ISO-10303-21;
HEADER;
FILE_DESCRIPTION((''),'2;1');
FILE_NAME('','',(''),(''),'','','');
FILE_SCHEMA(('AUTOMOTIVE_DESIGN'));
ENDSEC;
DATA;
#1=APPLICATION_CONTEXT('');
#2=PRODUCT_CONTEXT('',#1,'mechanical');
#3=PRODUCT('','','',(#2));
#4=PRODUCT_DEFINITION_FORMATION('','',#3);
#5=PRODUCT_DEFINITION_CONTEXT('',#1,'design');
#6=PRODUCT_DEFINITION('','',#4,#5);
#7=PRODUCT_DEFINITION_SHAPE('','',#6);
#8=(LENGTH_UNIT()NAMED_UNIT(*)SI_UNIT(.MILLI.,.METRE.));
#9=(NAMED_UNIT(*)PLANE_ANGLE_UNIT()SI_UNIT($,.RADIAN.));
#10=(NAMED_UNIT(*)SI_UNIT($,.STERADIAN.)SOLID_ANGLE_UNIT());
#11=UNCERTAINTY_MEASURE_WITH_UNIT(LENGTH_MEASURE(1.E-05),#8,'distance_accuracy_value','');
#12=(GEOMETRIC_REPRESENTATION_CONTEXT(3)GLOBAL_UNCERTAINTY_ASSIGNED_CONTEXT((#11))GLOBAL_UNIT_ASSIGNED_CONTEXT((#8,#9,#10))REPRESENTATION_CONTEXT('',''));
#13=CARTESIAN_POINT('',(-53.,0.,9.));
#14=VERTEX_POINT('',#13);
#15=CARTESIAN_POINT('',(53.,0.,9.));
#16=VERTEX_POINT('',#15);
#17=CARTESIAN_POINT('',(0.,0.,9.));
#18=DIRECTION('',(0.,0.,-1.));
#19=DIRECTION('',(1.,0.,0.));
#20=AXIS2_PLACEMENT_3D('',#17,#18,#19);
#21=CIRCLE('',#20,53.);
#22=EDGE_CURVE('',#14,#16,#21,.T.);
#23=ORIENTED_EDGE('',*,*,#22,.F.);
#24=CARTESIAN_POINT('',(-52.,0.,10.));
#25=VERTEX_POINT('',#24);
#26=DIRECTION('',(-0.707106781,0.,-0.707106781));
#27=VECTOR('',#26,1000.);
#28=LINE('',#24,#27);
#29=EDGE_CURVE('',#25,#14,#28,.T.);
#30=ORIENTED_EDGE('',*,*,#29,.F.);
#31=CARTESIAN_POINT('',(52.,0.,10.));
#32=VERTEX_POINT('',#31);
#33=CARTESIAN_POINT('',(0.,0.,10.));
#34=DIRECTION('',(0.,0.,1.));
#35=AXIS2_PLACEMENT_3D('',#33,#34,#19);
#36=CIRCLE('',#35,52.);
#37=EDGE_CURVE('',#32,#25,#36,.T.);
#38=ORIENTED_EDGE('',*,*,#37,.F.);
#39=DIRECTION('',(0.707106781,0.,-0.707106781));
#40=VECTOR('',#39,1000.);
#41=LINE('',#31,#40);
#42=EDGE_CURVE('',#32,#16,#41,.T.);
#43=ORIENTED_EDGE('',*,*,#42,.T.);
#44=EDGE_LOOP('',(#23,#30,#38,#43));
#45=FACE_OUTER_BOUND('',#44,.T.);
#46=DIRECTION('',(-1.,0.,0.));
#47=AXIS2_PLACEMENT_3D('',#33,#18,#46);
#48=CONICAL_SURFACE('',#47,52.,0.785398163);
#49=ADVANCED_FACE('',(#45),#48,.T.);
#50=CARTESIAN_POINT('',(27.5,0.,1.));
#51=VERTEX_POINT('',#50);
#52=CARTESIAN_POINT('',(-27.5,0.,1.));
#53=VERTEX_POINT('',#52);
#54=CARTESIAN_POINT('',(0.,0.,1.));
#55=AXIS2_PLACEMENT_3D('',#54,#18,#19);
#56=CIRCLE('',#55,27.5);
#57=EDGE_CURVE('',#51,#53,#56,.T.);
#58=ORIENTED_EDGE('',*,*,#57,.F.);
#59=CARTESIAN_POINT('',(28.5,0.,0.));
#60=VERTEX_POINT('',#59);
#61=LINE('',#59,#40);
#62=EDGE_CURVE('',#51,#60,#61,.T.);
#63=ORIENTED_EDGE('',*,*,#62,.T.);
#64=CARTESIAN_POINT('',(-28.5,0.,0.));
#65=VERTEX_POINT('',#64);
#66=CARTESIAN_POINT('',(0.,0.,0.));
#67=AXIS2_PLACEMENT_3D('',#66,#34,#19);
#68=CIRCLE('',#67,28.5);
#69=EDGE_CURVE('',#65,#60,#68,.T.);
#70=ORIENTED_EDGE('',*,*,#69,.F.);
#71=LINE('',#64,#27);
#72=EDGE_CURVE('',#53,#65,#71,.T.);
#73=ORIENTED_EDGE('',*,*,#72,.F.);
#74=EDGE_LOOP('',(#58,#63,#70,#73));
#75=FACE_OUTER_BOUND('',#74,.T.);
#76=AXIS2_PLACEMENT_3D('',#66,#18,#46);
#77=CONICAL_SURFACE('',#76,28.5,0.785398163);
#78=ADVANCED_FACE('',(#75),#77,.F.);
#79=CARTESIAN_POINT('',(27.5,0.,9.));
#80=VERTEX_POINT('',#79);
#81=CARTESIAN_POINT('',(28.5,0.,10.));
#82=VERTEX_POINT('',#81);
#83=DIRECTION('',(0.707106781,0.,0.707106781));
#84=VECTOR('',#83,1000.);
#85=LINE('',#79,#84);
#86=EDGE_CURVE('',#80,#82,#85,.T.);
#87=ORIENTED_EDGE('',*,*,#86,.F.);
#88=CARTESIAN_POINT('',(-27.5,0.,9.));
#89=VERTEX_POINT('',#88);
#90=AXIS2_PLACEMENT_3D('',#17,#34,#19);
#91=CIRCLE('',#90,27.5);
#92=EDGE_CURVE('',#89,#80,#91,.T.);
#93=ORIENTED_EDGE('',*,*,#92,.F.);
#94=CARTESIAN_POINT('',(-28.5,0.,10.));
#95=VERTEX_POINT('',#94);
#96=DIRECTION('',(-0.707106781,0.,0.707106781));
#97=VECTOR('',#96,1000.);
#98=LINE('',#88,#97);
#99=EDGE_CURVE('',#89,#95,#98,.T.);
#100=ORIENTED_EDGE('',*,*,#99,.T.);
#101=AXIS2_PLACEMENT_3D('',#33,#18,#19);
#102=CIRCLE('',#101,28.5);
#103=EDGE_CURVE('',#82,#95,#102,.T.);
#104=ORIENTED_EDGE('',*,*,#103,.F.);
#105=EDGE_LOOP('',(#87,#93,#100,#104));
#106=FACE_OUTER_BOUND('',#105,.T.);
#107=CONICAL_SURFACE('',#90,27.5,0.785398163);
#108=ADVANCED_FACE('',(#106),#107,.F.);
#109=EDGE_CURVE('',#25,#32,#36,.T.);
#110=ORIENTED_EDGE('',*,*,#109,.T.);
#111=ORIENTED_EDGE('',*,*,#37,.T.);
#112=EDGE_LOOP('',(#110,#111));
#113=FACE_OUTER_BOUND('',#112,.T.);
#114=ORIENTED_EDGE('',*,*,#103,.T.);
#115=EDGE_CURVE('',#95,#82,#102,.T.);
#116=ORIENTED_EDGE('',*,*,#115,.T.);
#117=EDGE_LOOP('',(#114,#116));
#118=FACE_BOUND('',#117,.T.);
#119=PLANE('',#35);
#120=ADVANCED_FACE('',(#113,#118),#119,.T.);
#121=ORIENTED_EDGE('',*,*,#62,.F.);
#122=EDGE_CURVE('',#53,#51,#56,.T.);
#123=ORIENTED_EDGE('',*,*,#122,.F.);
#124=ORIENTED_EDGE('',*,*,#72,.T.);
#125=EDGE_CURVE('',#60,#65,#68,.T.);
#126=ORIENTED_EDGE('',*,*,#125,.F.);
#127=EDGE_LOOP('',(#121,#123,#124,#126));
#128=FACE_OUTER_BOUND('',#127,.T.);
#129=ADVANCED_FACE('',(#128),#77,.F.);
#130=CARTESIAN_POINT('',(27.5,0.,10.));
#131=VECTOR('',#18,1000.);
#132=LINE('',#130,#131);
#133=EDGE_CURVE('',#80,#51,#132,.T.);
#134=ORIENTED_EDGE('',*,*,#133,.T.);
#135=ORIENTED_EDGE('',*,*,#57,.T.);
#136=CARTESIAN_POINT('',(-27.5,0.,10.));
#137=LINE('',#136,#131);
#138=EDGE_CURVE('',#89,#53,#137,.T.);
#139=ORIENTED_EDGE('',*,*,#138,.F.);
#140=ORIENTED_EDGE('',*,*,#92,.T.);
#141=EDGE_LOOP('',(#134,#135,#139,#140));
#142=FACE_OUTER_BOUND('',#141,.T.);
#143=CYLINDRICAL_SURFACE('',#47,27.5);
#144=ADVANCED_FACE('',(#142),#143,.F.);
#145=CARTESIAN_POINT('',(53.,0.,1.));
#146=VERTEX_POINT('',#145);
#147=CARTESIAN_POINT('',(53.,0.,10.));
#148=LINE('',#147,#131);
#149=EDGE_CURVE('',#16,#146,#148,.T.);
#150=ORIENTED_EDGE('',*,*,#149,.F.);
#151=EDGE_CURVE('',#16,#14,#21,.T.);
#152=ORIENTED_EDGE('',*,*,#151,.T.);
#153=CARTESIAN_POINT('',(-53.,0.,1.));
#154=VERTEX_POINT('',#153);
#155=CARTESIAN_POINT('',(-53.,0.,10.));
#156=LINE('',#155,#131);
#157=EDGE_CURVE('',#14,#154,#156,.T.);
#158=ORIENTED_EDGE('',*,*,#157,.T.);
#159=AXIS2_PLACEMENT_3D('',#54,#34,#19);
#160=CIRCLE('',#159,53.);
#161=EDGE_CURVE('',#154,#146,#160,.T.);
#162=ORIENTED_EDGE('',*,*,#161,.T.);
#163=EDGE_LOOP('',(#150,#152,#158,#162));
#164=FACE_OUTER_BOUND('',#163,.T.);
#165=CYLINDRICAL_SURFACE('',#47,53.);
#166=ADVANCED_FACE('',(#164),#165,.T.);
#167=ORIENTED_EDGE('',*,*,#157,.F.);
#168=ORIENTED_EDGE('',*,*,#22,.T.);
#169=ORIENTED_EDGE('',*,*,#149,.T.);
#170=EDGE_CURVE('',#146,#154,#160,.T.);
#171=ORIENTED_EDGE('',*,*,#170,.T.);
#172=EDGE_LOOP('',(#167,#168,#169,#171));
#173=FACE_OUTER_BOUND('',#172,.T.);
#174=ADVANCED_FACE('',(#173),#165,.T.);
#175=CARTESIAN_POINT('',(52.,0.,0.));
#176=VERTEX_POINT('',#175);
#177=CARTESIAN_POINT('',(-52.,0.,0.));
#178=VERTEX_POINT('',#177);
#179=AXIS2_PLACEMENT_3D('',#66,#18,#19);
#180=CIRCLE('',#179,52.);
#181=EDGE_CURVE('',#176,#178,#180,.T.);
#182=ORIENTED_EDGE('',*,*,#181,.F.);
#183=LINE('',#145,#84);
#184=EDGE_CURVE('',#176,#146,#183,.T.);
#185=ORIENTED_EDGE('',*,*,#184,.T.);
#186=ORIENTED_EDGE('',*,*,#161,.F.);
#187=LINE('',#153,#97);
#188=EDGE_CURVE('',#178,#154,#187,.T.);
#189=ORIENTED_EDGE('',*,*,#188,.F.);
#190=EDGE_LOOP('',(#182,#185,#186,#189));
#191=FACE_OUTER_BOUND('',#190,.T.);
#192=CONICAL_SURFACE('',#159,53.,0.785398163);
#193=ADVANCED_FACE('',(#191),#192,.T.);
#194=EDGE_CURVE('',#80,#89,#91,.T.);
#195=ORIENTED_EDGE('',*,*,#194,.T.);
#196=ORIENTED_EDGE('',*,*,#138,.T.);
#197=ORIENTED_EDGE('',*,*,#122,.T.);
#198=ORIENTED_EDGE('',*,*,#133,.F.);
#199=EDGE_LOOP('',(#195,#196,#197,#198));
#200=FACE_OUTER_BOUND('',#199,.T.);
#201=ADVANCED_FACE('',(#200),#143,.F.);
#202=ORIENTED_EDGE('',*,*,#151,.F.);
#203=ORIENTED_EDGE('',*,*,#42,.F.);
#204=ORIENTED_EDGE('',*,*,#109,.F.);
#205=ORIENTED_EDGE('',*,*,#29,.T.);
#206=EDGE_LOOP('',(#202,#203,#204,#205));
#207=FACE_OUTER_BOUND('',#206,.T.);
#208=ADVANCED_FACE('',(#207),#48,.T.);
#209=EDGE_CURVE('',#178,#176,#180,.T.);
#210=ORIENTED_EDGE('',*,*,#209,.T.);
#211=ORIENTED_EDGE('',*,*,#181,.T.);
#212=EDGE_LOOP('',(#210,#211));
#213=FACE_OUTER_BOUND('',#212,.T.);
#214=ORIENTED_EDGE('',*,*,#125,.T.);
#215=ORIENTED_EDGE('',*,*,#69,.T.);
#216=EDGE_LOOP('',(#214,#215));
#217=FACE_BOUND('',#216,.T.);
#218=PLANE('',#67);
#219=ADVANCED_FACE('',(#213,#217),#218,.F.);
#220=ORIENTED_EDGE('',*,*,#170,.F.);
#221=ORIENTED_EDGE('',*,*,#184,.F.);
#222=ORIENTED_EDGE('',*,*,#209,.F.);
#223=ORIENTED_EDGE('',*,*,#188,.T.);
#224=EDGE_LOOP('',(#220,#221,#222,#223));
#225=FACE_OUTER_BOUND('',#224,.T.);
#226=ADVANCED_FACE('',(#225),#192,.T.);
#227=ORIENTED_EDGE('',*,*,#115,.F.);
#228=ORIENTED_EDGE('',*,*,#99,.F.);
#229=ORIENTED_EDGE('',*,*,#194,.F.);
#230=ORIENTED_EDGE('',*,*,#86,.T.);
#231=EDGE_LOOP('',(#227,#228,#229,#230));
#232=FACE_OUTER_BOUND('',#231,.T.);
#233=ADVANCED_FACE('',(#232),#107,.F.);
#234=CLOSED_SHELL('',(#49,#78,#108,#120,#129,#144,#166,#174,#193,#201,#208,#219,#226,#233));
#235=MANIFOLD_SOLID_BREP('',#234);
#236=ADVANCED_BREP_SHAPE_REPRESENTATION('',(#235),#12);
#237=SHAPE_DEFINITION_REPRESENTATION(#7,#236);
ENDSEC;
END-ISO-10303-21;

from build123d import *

# Parameters (mm, degrees)
SKETCH1_R           = 53
SKETCH1_R_2         = 27.5
BOSS_EXTRUDE1_DEPTH = 10
CHAMFER1_SIZE       = 1


with BuildPart() as part:
    # Sketch1 → Boss-Extrude1 (new body)
    with BuildSketch(Plane.XY):
        Circle(SKETCH1_R)
        Circle(SKETCH1_R_2, mode=Mode.SUBTRACT)
    extrude(amount=BOSS_EXTRUDE1_DEPTH)

    # Chamfer1
    chamfer1_edges = [part.edges().sort_by_distance(p)[0] for p in [
        (-53, 0, 0),
        (-53, 0, 10),
        (-27.5, 0, 0),
        (-27.5, 0, 10),
    ]]
    chamfer(chamfer1_edges, length=CHAMFER1_SIZE)


solid = part.part
